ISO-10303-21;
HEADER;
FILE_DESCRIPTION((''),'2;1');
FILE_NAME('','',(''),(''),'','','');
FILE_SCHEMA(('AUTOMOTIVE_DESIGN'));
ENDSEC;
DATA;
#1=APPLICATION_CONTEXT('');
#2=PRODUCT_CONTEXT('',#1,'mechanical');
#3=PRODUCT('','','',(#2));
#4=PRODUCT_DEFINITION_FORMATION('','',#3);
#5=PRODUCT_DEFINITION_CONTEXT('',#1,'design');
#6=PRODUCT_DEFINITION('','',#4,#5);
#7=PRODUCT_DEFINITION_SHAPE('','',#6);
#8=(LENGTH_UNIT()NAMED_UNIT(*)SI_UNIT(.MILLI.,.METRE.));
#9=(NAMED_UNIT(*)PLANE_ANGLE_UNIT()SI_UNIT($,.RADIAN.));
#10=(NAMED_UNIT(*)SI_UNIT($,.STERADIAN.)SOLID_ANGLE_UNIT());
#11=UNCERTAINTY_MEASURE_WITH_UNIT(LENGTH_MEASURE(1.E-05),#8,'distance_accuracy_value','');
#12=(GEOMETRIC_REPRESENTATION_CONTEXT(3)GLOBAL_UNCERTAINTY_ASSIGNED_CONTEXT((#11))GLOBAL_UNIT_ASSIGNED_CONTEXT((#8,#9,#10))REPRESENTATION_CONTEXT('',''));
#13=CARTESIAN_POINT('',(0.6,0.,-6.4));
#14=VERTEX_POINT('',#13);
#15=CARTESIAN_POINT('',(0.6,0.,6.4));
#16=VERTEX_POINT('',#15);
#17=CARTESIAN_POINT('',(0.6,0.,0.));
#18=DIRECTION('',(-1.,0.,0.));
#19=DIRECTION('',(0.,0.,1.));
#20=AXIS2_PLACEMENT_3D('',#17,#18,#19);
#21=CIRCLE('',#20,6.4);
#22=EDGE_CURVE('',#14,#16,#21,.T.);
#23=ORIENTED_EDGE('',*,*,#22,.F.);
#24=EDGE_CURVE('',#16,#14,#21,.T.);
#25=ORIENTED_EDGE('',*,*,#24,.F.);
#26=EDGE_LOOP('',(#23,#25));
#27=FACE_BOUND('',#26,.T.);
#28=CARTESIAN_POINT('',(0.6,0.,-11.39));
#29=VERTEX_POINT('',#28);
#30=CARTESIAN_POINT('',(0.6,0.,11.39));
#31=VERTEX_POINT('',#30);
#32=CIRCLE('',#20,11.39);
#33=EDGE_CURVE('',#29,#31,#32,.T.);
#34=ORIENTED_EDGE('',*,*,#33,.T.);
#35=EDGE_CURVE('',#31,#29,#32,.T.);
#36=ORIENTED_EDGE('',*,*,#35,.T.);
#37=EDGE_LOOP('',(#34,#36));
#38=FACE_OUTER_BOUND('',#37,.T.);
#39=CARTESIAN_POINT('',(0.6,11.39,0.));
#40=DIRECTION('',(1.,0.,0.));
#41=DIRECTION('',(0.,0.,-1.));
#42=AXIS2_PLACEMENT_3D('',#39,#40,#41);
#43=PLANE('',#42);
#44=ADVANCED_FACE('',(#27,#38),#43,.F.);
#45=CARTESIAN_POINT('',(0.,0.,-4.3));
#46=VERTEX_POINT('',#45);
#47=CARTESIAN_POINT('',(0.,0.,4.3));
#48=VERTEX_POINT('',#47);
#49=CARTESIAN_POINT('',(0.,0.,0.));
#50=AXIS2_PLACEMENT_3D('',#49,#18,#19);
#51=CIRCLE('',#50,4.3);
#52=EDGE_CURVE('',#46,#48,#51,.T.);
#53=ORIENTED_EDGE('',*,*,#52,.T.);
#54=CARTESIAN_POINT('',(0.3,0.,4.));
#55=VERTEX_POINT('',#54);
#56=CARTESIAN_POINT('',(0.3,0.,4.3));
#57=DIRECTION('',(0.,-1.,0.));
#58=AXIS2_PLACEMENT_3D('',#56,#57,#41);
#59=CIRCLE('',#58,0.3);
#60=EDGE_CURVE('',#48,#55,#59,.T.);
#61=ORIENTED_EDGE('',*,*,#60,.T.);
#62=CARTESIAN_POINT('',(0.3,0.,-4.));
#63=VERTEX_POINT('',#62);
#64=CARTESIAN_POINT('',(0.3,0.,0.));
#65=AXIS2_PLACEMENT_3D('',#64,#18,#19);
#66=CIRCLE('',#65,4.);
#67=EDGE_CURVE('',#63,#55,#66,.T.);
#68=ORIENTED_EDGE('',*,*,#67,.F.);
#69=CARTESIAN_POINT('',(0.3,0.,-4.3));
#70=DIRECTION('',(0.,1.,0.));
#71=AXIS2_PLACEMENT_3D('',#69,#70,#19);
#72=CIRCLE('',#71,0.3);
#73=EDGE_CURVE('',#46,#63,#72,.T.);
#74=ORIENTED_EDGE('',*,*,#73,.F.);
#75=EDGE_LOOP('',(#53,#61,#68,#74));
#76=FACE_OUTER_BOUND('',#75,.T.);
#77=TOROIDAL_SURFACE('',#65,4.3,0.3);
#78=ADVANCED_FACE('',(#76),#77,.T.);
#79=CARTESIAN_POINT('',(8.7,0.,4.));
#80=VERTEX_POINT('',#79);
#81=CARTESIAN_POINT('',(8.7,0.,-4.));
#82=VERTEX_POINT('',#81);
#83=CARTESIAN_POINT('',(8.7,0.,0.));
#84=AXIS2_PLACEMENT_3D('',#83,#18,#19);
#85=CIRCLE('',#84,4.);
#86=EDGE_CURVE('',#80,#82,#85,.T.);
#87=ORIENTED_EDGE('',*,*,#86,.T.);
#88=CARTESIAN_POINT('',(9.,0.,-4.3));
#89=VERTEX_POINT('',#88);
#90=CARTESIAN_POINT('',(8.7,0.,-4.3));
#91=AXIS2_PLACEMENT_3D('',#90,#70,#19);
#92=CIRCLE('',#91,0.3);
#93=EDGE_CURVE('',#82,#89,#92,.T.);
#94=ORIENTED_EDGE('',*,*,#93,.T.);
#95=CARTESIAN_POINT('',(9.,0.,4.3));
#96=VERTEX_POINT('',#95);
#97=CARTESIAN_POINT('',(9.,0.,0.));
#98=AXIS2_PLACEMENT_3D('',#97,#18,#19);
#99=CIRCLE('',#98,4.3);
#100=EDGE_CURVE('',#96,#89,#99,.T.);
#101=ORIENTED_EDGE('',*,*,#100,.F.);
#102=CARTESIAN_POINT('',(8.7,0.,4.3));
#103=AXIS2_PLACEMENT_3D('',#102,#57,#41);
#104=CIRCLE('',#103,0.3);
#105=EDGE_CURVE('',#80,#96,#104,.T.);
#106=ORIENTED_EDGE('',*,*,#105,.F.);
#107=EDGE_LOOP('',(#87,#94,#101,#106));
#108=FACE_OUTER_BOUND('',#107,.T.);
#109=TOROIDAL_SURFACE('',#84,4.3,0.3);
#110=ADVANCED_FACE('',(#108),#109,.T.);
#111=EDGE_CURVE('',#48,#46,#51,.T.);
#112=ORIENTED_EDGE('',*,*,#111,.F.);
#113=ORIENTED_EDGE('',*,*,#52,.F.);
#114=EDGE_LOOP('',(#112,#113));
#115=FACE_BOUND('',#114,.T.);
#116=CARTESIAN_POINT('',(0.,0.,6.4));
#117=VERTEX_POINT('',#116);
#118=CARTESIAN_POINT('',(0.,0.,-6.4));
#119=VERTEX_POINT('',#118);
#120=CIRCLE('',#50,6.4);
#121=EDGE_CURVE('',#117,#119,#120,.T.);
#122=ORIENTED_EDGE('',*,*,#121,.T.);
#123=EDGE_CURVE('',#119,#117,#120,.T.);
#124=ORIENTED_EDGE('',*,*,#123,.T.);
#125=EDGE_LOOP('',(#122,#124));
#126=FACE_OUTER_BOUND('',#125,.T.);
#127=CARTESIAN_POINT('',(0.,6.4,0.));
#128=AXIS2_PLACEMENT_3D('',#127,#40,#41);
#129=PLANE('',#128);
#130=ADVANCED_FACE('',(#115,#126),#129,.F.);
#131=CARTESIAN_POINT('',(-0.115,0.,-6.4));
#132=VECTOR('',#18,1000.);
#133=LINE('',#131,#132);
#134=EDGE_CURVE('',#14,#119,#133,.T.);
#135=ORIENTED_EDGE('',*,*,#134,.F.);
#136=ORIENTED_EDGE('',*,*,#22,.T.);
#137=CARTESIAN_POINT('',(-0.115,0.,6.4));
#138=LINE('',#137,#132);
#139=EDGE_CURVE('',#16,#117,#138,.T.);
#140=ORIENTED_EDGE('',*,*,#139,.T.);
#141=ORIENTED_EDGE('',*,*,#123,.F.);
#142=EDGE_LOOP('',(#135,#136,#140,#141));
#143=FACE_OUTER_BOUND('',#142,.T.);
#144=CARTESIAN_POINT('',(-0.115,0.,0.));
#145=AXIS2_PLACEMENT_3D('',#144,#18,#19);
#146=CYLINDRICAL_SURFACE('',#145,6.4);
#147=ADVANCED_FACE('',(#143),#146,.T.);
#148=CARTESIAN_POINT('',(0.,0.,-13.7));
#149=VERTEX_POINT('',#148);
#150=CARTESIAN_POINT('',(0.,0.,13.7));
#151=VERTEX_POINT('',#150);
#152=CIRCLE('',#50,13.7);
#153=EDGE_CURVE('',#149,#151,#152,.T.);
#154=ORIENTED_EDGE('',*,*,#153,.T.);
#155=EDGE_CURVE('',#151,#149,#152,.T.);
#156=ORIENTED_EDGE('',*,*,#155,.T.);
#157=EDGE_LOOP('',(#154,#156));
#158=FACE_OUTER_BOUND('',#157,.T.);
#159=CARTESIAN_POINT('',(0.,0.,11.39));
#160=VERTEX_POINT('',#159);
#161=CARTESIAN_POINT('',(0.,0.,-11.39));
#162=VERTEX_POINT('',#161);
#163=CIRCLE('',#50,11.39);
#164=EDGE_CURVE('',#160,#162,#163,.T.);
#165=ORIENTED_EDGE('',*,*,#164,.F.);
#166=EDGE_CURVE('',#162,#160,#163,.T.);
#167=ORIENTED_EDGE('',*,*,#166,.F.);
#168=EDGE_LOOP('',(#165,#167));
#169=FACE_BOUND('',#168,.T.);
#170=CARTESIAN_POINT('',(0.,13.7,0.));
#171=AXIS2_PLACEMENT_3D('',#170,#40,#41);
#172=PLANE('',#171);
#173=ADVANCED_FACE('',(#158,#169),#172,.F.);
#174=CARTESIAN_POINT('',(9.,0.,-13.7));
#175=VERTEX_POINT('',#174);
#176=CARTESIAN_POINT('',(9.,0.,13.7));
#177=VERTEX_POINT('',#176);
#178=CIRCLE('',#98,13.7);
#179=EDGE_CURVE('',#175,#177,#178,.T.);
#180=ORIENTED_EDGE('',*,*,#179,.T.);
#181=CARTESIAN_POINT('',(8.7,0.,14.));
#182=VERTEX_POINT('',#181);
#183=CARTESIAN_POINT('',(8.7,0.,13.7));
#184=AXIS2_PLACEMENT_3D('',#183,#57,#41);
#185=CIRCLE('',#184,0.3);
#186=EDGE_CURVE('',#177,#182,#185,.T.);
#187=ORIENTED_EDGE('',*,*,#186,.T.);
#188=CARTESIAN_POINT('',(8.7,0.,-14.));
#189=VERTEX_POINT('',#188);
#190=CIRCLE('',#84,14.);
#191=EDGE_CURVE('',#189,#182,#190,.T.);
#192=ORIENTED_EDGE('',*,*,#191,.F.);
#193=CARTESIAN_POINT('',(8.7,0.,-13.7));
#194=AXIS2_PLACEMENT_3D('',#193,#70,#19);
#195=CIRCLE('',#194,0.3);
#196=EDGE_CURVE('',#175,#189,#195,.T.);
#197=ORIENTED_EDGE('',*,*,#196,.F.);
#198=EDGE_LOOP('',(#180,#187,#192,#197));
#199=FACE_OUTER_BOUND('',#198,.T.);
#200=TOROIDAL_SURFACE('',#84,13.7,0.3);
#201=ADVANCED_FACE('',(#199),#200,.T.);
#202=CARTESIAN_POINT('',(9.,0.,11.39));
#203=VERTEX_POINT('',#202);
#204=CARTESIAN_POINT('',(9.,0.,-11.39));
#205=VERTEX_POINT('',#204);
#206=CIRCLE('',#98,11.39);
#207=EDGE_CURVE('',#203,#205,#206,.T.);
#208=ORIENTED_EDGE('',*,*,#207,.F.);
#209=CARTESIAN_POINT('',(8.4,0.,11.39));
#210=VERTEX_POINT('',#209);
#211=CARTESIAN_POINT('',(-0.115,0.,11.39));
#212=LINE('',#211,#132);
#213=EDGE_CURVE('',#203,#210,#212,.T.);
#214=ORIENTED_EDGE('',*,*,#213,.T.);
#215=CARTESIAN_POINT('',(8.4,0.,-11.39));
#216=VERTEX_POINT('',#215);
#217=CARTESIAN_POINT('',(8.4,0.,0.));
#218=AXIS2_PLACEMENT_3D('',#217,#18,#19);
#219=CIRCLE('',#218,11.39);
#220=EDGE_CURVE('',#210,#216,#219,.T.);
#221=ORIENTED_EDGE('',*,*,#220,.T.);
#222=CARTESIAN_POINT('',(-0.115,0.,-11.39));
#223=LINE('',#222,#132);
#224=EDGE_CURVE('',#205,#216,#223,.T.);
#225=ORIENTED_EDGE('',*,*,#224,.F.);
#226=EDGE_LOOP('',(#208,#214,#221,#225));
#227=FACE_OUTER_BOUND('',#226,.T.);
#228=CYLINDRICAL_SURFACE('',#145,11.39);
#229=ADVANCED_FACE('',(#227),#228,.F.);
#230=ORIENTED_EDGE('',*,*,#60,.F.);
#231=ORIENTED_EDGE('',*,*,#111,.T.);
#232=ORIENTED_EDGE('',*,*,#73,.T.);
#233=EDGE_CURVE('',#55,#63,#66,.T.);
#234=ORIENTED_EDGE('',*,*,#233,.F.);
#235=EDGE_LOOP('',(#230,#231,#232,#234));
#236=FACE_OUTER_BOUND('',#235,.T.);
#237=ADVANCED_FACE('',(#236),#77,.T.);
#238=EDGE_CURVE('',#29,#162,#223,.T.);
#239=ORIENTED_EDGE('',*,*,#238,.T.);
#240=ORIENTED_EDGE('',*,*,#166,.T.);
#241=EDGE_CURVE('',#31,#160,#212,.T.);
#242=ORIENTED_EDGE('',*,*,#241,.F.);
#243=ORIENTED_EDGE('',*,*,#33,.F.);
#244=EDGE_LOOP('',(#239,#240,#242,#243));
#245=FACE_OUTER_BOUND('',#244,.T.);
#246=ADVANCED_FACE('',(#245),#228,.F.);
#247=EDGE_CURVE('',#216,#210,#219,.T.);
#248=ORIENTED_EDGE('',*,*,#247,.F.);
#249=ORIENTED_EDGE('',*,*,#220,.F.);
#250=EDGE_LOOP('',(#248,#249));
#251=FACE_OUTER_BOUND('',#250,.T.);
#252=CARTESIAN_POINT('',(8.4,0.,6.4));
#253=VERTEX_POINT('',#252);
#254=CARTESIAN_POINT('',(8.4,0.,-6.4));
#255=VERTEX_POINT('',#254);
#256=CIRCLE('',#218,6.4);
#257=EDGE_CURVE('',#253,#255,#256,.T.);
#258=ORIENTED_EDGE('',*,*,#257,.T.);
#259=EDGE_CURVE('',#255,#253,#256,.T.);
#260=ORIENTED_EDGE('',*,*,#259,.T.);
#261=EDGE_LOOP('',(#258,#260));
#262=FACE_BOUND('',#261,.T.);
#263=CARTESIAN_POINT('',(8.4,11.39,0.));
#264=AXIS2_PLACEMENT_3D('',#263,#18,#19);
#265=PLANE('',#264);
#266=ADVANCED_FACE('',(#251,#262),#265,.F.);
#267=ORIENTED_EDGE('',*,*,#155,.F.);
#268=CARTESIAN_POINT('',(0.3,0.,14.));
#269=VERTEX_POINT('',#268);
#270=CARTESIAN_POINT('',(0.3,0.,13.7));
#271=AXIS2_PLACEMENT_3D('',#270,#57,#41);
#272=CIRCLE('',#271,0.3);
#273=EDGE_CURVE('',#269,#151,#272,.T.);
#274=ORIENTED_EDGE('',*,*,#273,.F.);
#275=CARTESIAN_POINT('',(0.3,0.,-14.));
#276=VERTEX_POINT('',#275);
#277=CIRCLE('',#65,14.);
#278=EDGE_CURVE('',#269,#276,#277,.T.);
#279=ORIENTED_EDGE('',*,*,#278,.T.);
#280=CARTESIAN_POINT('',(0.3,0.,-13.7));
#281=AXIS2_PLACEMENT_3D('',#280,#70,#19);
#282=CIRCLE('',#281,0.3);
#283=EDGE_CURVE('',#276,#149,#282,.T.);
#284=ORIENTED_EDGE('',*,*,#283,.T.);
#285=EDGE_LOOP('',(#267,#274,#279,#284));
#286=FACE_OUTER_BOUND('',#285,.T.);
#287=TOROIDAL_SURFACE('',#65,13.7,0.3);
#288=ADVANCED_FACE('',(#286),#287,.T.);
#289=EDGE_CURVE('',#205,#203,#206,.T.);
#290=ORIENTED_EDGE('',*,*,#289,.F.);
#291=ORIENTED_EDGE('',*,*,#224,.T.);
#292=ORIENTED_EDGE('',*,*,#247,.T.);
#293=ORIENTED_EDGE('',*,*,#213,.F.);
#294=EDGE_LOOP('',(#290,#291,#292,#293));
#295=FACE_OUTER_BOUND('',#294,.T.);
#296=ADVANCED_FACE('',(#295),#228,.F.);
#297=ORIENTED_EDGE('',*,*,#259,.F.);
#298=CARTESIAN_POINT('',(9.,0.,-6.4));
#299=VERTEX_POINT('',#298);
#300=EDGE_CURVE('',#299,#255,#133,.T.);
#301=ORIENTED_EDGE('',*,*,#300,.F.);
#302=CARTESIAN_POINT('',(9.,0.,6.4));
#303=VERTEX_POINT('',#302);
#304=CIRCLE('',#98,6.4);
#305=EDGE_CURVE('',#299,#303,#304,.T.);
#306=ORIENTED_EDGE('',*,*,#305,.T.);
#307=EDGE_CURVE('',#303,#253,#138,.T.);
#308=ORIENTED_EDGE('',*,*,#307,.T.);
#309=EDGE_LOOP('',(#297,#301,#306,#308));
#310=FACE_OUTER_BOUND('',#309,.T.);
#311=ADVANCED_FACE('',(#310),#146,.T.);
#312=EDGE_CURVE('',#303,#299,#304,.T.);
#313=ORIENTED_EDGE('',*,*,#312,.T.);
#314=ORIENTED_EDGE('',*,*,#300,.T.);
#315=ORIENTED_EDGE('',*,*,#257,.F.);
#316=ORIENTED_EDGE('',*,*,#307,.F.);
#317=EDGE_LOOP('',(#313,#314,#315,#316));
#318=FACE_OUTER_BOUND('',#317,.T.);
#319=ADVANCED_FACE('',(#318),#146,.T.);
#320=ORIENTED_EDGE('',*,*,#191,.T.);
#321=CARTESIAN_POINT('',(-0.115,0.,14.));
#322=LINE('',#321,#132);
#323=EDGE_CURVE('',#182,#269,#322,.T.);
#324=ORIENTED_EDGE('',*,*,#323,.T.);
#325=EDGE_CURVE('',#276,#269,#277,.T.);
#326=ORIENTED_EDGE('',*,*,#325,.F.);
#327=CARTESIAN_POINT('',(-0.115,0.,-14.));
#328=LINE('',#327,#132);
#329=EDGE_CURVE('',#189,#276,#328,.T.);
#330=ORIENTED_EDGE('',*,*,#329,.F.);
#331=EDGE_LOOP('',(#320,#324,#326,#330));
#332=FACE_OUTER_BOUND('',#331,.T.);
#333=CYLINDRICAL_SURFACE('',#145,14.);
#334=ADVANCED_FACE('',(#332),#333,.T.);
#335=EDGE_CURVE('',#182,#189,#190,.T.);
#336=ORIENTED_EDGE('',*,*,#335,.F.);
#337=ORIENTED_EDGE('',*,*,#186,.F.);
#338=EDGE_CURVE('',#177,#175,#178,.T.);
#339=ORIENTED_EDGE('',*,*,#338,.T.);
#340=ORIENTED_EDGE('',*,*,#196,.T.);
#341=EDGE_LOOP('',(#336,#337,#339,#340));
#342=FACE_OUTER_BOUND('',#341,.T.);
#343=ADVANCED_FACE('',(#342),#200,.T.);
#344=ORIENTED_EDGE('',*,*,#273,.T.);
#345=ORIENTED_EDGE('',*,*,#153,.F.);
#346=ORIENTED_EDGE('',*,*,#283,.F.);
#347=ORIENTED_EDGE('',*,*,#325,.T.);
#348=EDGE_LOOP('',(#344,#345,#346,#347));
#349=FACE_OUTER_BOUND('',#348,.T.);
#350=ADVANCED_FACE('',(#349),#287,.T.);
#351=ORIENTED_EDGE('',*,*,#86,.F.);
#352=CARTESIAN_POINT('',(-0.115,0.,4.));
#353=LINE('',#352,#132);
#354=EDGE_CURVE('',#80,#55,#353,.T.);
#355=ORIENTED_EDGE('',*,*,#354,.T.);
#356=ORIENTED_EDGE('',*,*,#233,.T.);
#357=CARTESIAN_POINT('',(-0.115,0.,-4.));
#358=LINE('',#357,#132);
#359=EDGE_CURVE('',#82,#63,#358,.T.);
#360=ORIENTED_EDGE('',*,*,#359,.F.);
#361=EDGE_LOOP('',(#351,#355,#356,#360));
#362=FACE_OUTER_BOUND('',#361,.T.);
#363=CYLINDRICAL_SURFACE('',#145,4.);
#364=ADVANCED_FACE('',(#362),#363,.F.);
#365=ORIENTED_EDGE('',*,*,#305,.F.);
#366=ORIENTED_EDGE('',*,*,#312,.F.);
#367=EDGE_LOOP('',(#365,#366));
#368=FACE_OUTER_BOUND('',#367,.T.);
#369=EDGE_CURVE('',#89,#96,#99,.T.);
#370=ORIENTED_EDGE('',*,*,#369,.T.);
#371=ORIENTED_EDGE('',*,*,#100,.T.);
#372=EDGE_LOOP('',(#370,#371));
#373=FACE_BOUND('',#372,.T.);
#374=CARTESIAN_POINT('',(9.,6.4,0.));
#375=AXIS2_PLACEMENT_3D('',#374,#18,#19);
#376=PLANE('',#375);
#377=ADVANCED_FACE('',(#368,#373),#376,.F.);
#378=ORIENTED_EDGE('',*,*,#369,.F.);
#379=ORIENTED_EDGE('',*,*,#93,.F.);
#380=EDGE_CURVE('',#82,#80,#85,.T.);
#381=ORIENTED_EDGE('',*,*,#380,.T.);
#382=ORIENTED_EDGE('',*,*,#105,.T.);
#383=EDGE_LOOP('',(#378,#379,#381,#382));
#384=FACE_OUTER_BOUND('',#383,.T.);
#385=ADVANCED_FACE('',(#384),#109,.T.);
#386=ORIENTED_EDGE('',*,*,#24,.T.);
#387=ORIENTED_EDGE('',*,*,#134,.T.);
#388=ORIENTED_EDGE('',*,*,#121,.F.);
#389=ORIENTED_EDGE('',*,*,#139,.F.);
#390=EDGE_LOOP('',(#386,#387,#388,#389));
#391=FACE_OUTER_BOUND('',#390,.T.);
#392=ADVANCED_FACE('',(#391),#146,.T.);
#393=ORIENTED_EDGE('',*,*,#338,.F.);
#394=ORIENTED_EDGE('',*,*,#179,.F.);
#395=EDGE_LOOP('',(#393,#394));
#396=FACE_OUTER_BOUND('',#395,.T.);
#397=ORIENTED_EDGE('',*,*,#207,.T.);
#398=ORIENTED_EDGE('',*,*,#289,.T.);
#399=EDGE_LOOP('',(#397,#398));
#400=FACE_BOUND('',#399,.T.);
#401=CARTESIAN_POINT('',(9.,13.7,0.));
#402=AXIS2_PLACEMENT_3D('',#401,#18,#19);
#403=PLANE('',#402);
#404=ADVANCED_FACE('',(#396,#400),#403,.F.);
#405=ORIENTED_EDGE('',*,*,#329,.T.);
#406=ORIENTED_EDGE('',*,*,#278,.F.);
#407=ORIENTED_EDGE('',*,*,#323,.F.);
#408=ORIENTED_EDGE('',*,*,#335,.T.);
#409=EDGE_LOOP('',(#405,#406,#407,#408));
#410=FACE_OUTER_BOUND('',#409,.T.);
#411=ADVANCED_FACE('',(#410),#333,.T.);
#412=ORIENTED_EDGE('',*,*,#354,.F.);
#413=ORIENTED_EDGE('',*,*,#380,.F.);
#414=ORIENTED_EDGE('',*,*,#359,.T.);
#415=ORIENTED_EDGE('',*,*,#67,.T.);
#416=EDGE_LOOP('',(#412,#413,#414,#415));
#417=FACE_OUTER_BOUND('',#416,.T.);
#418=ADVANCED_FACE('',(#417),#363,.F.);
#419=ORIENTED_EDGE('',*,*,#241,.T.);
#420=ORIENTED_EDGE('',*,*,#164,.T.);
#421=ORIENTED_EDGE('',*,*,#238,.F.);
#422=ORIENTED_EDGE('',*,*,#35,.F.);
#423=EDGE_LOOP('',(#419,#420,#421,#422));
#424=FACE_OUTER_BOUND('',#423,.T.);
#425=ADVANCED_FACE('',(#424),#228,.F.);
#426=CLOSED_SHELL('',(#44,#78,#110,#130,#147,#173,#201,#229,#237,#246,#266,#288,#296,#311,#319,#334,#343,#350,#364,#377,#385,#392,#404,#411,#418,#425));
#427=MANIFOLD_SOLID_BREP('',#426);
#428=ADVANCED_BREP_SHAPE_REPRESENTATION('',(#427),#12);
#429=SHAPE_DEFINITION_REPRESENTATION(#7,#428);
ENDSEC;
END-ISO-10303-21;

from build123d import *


with BuildPart() as part:
    # Sketch1 → Revolve1 (revolve)
    with BuildSketch(Plane.XY, mode=Mode.PRIVATE) as revolve1_sk:
        with BuildLine():
            Line((0, 11.39), (0.6, 11.39))
            Line((0.6, 11.39), (0.6, 6.4))
            Line((0.6, 6.4), (0, 6.4))
            Line((0, 6.4), (0, 4.3))
            ThreePointArc((0, 4.3), (0.087867966, 4.087867966), (0.3, 4))
            Line((0.3, 4), (8.7, 4))
            ThreePointArc((8.7, 4), (8.912132034, 4.087867966), (9, 4.3))
            Line((9, 4.3), (9, 6.4))
            Line((9, 6.4), (8.4, 6.4))
            Line((8.4, 6.4), (8.4, 11.39))
            Line((8.4, 11.39), (9, 11.39))
            Line((9, 11.39), (9, 13.7))
            ThreePointArc((9, 13.7), (8.912132034, 13.912132034), (8.7, 14))
            Line((8.7, 14), (0.3, 14))
            ThreePointArc((0.3, 14), (0.087867966, 13.912132034), (0, 13.7))
            Line((0, 13.7), (0, 11.39))
        make_face()
    revolve(revolve1_sk.sketch.rotate(Axis((-0.115, 0, 0), (1, 0, 0)), 90), axis=Axis((-0.115, 0, 0), (1, 0, 0)))


solid = part.part
